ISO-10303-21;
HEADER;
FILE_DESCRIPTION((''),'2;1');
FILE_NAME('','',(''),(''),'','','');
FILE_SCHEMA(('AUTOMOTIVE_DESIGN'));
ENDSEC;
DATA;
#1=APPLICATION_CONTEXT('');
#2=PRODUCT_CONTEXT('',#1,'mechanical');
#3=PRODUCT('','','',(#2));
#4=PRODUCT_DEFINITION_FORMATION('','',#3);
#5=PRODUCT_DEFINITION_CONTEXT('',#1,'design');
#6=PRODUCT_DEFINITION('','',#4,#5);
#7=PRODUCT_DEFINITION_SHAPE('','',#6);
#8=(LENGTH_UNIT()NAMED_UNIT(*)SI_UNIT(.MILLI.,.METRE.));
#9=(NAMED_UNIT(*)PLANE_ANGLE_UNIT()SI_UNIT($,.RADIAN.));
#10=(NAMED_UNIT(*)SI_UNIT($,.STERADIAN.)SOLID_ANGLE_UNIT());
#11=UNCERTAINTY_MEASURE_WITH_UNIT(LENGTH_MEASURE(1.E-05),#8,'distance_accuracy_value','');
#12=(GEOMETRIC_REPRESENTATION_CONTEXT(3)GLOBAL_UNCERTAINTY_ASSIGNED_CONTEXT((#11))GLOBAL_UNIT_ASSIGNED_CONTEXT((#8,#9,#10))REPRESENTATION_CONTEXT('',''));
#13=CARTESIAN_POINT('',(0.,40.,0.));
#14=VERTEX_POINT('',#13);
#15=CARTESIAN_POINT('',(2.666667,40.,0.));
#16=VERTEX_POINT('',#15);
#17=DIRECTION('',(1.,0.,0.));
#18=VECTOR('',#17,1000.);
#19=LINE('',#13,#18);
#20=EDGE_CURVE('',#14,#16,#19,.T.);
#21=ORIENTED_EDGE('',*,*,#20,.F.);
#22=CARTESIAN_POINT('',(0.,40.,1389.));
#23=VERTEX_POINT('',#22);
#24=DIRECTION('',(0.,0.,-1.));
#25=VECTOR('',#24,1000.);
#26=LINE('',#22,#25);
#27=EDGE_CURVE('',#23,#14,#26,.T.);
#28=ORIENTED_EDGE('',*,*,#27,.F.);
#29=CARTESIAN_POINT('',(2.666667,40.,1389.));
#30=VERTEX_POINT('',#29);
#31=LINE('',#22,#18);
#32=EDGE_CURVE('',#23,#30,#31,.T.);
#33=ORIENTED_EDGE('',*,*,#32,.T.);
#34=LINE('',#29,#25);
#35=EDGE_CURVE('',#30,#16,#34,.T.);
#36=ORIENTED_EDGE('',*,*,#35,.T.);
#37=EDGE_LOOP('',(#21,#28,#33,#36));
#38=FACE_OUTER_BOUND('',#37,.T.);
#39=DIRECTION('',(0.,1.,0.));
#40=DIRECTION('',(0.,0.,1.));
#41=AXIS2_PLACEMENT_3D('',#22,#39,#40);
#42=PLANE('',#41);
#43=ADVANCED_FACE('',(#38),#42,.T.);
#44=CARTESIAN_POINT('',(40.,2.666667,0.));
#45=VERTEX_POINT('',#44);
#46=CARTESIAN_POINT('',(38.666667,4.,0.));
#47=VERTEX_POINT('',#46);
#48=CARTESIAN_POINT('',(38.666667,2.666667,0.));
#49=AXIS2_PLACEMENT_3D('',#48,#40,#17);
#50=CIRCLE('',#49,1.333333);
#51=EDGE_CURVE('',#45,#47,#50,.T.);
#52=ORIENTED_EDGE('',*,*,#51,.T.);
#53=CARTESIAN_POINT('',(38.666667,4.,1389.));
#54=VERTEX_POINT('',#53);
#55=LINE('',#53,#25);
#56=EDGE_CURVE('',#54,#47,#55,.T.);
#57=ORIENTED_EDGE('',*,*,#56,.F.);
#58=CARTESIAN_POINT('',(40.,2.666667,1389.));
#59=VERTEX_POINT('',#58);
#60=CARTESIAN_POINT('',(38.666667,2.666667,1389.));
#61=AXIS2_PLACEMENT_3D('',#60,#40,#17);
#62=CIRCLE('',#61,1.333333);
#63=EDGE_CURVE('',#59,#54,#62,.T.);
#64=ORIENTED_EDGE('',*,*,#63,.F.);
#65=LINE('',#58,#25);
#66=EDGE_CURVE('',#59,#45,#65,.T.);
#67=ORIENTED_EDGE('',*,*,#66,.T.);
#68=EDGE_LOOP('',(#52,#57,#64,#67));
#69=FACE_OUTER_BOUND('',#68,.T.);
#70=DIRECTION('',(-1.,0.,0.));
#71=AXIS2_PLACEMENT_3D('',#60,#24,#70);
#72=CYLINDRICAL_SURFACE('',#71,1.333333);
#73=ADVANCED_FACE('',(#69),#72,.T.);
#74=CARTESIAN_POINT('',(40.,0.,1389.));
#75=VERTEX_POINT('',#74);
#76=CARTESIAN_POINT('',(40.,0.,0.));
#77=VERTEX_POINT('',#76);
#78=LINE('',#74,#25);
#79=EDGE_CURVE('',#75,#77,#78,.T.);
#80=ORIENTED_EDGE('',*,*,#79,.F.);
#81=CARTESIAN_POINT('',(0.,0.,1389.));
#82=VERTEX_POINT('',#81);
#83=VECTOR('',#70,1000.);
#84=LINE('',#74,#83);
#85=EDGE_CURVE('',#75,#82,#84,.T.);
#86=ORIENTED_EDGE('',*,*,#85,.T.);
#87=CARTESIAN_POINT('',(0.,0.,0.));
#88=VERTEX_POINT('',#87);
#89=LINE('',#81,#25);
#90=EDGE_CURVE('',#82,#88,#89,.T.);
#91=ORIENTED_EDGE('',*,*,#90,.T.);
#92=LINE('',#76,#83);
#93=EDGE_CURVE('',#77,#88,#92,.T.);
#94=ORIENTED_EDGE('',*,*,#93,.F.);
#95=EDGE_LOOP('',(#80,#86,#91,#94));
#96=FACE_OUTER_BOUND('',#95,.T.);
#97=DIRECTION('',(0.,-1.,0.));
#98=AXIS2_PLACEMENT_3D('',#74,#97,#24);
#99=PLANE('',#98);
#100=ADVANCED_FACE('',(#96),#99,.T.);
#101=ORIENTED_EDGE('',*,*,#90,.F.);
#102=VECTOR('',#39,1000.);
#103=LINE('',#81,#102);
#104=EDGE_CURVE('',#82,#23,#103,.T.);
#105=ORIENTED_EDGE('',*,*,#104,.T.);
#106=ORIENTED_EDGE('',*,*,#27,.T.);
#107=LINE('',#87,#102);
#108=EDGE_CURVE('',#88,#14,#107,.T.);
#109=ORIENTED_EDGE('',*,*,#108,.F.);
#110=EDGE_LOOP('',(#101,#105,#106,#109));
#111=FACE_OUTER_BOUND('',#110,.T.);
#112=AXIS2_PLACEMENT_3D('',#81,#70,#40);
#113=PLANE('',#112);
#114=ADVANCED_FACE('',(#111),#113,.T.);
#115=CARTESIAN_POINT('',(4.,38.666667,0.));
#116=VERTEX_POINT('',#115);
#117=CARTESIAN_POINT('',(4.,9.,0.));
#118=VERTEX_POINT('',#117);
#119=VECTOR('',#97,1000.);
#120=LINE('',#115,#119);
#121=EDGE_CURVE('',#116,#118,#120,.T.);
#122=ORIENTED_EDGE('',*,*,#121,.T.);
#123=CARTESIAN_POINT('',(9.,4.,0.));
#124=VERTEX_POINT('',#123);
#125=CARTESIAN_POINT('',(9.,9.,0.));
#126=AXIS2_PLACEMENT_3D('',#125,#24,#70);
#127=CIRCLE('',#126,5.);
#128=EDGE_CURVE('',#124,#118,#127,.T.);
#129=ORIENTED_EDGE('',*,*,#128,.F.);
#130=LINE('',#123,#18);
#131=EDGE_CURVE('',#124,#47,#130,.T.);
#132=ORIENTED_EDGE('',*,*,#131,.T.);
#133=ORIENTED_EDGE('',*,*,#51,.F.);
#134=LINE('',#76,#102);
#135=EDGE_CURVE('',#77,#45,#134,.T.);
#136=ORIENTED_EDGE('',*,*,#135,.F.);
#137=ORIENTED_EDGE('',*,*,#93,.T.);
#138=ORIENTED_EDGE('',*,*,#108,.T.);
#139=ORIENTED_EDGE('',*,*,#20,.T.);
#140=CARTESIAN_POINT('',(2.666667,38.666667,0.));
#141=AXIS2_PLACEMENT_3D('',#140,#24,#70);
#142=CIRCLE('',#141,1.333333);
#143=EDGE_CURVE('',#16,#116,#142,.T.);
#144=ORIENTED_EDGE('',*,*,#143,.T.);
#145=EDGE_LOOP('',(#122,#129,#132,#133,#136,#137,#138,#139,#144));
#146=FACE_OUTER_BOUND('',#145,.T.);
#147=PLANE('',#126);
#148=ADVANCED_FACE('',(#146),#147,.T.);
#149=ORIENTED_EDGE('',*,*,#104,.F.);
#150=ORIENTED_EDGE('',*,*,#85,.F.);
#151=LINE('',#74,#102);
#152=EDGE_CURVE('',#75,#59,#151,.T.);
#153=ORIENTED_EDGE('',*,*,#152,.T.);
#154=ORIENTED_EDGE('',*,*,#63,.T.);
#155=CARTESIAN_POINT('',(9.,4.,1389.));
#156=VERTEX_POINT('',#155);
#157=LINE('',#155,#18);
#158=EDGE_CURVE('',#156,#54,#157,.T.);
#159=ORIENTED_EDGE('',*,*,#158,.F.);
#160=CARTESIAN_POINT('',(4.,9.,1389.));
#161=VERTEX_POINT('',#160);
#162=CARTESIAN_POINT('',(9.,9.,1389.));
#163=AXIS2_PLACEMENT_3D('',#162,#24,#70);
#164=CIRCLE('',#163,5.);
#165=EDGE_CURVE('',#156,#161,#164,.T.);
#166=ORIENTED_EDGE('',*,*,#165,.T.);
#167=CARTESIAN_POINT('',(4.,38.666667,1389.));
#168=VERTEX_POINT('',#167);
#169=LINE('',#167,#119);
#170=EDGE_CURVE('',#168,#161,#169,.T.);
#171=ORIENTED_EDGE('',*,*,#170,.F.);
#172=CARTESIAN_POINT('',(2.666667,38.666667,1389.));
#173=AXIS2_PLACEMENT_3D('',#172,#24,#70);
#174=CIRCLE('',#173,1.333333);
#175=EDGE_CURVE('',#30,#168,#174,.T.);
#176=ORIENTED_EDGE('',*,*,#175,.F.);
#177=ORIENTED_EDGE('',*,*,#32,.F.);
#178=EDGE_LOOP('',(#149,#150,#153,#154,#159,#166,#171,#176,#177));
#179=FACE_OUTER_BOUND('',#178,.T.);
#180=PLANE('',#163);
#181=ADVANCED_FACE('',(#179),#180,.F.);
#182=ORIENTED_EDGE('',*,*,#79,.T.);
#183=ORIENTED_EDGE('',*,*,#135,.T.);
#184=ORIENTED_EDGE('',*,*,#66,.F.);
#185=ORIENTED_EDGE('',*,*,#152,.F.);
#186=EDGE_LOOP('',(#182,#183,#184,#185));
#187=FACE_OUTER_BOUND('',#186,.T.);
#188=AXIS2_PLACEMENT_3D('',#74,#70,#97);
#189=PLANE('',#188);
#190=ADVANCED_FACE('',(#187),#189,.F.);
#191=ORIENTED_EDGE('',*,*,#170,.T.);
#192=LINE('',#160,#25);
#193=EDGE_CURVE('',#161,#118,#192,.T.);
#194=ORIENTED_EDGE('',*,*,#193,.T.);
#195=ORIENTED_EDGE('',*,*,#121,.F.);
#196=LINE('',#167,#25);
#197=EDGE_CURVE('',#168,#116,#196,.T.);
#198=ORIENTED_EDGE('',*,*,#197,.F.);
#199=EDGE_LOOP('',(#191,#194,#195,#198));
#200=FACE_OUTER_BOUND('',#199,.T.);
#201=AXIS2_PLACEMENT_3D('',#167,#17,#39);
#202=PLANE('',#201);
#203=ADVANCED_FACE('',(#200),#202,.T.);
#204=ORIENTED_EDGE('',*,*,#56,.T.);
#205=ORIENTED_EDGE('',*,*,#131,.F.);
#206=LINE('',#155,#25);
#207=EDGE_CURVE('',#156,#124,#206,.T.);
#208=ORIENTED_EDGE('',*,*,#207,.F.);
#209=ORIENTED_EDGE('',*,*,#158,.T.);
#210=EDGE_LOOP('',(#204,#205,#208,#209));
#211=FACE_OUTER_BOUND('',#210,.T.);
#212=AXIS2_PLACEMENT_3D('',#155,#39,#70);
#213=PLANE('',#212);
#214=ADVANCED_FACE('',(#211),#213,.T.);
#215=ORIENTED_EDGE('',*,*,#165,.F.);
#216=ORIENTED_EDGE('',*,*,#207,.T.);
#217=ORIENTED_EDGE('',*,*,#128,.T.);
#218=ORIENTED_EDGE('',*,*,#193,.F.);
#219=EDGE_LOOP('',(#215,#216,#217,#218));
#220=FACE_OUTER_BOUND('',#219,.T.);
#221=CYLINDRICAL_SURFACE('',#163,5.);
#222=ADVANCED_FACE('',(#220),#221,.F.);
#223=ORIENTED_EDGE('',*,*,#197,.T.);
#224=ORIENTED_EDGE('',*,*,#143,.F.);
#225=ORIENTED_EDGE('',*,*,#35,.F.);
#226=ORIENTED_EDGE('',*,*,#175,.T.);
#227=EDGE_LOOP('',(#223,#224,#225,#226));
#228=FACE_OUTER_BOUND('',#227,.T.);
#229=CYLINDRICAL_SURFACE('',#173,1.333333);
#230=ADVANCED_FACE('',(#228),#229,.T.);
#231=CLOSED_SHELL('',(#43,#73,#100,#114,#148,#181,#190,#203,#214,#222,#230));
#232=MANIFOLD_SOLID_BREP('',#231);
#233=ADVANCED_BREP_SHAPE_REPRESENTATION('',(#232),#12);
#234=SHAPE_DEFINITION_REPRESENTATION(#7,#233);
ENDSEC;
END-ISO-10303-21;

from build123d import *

# Parameters (mm, degrees)
BOSS_EXTRUDE1_DEPTH = 1389


with BuildPart() as part:
    # Sketch1 → Boss-Extrude1 (new body)
    with BuildSketch(Plane.XY):
        with BuildLine():
            Line((0, 0), (0, 40))
            Line((0, 40), (2.666666667, 40))
            ThreePointArc((2.666666667, 40), (3.609475708, 39.609475708), (4, 38.666666667))
            Line((4, 38.666666667), (4, 9))
            ThreePointArc((4, 9), (5.464466094, 5.464466094), (9, 4))
            Line((9, 4), (38.666666667, 4))
            ThreePointArc((38.666666667, 4), (39.609475708, 3.609475708), (40, 2.666666667))
            Line((40, 2.666666667), (40, 0))
            Line((40, 0), (0, 0))
        make_face()
    extrude(amount=BOSS_EXTRUDE1_DEPTH)


solid = part.part
